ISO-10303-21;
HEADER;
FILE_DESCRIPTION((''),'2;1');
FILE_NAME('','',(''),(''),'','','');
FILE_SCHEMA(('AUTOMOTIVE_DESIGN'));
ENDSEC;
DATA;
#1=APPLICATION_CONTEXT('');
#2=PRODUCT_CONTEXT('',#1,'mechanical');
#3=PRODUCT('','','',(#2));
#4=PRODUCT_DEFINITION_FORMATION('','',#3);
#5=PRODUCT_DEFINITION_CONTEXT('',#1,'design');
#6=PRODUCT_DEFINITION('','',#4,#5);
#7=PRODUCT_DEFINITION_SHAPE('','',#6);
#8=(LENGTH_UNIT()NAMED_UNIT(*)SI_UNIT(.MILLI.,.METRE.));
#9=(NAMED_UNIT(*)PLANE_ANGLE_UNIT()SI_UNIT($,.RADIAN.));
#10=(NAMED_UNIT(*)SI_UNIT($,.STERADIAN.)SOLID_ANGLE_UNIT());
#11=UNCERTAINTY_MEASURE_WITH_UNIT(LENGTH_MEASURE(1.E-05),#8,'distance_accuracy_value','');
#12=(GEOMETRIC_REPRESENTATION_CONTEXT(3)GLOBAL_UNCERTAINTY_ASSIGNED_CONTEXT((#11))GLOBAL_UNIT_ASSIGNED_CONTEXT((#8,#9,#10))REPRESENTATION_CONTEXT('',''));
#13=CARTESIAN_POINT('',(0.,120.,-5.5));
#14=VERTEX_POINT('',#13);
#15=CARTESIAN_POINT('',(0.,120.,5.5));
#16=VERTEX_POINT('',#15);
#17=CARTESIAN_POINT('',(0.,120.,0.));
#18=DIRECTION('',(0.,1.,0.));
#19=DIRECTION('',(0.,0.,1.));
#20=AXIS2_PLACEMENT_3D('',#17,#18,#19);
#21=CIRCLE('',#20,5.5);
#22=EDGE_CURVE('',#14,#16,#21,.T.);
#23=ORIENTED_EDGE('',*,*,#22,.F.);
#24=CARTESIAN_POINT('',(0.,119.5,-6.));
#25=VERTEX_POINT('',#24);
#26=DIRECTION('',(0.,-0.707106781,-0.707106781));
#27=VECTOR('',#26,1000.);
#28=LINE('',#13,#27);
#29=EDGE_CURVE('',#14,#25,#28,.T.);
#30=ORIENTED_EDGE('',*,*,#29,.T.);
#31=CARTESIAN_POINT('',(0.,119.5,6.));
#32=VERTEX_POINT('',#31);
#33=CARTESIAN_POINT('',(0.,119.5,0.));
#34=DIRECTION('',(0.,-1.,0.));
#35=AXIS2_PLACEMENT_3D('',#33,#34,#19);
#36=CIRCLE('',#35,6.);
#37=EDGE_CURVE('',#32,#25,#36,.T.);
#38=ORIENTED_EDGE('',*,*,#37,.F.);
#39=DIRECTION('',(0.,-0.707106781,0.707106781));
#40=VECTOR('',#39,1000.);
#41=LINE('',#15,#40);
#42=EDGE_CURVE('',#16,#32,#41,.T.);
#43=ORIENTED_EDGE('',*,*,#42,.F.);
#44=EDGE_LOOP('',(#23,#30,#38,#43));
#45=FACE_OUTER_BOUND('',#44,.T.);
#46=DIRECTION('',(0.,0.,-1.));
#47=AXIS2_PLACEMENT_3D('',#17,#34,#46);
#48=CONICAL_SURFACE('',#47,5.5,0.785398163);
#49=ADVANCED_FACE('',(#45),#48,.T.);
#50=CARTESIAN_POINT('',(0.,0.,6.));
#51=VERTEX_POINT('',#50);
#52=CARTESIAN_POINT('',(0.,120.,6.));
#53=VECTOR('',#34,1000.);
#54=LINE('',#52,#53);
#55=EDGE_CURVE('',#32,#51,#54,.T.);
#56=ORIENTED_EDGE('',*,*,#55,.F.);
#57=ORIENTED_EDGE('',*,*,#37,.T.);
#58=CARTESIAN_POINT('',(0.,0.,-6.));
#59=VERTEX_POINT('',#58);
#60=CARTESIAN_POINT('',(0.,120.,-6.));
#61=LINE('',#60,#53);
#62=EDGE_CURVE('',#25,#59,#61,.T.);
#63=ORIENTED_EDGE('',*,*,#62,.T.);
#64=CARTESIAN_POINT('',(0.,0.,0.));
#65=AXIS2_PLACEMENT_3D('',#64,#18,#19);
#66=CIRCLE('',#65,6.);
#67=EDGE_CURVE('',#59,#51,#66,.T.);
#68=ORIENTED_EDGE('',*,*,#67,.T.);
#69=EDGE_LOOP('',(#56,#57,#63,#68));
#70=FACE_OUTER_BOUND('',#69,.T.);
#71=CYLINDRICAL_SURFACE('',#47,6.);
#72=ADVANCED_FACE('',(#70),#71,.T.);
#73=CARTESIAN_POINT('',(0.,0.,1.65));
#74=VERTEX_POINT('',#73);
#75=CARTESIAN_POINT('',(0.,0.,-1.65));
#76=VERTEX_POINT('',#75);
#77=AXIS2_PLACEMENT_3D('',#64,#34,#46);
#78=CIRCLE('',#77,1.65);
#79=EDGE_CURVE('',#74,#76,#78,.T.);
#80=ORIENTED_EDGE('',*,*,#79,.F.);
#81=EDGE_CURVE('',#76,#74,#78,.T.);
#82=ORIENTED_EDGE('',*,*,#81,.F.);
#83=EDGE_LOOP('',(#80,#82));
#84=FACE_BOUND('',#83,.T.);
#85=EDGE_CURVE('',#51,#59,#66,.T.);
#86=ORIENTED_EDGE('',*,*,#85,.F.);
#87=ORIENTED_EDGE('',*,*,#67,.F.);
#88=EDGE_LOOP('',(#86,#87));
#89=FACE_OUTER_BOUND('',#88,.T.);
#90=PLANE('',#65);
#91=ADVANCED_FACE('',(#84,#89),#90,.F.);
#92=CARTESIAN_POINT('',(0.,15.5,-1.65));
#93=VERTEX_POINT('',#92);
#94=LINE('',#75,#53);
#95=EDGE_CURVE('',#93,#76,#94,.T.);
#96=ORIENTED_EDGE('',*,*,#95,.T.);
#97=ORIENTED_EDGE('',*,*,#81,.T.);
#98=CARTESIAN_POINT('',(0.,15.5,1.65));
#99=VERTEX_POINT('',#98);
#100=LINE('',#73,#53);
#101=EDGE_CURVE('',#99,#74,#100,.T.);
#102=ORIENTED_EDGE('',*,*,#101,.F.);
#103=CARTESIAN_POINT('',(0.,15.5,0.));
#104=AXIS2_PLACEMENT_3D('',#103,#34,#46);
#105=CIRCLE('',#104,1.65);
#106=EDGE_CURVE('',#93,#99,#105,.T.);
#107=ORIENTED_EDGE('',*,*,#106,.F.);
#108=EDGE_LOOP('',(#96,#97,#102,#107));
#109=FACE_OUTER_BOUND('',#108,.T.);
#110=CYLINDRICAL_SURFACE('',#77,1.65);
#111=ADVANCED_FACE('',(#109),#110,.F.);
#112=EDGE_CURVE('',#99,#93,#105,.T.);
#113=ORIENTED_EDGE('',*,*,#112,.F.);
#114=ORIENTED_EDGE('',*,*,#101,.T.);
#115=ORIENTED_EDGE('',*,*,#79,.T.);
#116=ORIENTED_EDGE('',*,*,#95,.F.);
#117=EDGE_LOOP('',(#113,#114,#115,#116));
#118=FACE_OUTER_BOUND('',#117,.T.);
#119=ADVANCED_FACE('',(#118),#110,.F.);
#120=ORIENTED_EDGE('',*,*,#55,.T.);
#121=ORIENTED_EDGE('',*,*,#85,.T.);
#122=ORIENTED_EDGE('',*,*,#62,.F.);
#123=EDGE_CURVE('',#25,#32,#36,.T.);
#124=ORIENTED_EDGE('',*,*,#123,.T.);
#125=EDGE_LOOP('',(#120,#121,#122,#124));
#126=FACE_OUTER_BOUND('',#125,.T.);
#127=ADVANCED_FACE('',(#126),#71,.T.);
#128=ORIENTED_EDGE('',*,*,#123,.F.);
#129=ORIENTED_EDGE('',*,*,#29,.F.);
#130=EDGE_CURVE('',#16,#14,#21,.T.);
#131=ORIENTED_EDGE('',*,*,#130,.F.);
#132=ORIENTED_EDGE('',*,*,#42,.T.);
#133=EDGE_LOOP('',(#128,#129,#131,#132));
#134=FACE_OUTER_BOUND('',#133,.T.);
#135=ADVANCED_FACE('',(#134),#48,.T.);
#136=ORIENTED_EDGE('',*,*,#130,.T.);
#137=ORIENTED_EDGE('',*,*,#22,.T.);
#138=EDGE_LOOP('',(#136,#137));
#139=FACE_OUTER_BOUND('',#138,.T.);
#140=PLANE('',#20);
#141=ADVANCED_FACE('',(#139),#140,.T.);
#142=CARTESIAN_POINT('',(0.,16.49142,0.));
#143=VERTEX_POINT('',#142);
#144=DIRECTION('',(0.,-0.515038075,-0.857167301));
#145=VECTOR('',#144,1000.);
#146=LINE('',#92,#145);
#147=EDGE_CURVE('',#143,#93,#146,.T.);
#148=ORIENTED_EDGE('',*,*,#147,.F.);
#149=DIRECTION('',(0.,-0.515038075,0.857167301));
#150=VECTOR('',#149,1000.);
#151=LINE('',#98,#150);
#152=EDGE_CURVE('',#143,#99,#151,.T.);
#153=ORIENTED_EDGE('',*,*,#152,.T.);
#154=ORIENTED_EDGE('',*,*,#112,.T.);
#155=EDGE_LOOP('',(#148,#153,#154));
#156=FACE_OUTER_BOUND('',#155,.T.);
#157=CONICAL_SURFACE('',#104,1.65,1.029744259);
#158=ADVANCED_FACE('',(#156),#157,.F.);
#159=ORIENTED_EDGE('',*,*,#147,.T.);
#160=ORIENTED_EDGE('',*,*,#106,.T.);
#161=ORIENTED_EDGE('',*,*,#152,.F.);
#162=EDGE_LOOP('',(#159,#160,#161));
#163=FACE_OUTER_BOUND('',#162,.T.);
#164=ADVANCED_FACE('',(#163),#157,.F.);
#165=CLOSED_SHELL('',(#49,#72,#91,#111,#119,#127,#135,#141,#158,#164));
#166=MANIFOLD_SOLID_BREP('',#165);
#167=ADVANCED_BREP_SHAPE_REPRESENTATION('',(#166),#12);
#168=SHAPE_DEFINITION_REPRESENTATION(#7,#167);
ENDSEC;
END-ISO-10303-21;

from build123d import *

# Parameters (mm, degrees)
SKETCH_1_R             = 6
EXTRUDE_1_DEPTH        = 120
HOLE_WIZARD_M4_1_D     = 3.3
HOLE_WIZARD_M4_1_DEPTH = 15.5
HOLE_WIZARD_M4_1_TIP   = 0.991420021
CHAMFER_1_SIZE         = 0.5


with BuildPart() as part:
    # 草图1 → 凸台-拉伸1 (new body)
    with BuildSketch(Plane(origin=(0, 0, 0), x_dir=(1, 0, 0), z_dir=(0, 1, 0))):
        with Locations(Location((0, 0, 0), (0, 0, 270))):
            Circle(SKETCH_1_R)
    extrude(amount=EXTRUDE_1_DEPTH)

    # M4 螺纹孔1
    with Locations(Plane(origin=(0, 0, 0), x_dir=(-1, 0, 0), z_dir=(0, -1, 0))):
        with Locations((0, 0)):
            Hole(HOLE_WIZARD_M4_1_D / 2, depth=HOLE_WIZARD_M4_1_DEPTH)
            with Locations((0, 0, -(HOLE_WIZARD_M4_1_DEPTH + HOLE_WIZARD_M4_1_TIP / 2))):  # 118° drill point
                Cone(0, HOLE_WIZARD_M4_1_D / 2, HOLE_WIZARD_M4_1_TIP, mode=Mode.SUBTRACT)

    # 倒角1
    chamfer_1_edges = [part.edges().sort_by_distance(p)[0] for p in [
        (0, 120, -6),
    ]]
    chamfer(chamfer_1_edges, length=CHAMFER_1_SIZE)


solid = part.part
